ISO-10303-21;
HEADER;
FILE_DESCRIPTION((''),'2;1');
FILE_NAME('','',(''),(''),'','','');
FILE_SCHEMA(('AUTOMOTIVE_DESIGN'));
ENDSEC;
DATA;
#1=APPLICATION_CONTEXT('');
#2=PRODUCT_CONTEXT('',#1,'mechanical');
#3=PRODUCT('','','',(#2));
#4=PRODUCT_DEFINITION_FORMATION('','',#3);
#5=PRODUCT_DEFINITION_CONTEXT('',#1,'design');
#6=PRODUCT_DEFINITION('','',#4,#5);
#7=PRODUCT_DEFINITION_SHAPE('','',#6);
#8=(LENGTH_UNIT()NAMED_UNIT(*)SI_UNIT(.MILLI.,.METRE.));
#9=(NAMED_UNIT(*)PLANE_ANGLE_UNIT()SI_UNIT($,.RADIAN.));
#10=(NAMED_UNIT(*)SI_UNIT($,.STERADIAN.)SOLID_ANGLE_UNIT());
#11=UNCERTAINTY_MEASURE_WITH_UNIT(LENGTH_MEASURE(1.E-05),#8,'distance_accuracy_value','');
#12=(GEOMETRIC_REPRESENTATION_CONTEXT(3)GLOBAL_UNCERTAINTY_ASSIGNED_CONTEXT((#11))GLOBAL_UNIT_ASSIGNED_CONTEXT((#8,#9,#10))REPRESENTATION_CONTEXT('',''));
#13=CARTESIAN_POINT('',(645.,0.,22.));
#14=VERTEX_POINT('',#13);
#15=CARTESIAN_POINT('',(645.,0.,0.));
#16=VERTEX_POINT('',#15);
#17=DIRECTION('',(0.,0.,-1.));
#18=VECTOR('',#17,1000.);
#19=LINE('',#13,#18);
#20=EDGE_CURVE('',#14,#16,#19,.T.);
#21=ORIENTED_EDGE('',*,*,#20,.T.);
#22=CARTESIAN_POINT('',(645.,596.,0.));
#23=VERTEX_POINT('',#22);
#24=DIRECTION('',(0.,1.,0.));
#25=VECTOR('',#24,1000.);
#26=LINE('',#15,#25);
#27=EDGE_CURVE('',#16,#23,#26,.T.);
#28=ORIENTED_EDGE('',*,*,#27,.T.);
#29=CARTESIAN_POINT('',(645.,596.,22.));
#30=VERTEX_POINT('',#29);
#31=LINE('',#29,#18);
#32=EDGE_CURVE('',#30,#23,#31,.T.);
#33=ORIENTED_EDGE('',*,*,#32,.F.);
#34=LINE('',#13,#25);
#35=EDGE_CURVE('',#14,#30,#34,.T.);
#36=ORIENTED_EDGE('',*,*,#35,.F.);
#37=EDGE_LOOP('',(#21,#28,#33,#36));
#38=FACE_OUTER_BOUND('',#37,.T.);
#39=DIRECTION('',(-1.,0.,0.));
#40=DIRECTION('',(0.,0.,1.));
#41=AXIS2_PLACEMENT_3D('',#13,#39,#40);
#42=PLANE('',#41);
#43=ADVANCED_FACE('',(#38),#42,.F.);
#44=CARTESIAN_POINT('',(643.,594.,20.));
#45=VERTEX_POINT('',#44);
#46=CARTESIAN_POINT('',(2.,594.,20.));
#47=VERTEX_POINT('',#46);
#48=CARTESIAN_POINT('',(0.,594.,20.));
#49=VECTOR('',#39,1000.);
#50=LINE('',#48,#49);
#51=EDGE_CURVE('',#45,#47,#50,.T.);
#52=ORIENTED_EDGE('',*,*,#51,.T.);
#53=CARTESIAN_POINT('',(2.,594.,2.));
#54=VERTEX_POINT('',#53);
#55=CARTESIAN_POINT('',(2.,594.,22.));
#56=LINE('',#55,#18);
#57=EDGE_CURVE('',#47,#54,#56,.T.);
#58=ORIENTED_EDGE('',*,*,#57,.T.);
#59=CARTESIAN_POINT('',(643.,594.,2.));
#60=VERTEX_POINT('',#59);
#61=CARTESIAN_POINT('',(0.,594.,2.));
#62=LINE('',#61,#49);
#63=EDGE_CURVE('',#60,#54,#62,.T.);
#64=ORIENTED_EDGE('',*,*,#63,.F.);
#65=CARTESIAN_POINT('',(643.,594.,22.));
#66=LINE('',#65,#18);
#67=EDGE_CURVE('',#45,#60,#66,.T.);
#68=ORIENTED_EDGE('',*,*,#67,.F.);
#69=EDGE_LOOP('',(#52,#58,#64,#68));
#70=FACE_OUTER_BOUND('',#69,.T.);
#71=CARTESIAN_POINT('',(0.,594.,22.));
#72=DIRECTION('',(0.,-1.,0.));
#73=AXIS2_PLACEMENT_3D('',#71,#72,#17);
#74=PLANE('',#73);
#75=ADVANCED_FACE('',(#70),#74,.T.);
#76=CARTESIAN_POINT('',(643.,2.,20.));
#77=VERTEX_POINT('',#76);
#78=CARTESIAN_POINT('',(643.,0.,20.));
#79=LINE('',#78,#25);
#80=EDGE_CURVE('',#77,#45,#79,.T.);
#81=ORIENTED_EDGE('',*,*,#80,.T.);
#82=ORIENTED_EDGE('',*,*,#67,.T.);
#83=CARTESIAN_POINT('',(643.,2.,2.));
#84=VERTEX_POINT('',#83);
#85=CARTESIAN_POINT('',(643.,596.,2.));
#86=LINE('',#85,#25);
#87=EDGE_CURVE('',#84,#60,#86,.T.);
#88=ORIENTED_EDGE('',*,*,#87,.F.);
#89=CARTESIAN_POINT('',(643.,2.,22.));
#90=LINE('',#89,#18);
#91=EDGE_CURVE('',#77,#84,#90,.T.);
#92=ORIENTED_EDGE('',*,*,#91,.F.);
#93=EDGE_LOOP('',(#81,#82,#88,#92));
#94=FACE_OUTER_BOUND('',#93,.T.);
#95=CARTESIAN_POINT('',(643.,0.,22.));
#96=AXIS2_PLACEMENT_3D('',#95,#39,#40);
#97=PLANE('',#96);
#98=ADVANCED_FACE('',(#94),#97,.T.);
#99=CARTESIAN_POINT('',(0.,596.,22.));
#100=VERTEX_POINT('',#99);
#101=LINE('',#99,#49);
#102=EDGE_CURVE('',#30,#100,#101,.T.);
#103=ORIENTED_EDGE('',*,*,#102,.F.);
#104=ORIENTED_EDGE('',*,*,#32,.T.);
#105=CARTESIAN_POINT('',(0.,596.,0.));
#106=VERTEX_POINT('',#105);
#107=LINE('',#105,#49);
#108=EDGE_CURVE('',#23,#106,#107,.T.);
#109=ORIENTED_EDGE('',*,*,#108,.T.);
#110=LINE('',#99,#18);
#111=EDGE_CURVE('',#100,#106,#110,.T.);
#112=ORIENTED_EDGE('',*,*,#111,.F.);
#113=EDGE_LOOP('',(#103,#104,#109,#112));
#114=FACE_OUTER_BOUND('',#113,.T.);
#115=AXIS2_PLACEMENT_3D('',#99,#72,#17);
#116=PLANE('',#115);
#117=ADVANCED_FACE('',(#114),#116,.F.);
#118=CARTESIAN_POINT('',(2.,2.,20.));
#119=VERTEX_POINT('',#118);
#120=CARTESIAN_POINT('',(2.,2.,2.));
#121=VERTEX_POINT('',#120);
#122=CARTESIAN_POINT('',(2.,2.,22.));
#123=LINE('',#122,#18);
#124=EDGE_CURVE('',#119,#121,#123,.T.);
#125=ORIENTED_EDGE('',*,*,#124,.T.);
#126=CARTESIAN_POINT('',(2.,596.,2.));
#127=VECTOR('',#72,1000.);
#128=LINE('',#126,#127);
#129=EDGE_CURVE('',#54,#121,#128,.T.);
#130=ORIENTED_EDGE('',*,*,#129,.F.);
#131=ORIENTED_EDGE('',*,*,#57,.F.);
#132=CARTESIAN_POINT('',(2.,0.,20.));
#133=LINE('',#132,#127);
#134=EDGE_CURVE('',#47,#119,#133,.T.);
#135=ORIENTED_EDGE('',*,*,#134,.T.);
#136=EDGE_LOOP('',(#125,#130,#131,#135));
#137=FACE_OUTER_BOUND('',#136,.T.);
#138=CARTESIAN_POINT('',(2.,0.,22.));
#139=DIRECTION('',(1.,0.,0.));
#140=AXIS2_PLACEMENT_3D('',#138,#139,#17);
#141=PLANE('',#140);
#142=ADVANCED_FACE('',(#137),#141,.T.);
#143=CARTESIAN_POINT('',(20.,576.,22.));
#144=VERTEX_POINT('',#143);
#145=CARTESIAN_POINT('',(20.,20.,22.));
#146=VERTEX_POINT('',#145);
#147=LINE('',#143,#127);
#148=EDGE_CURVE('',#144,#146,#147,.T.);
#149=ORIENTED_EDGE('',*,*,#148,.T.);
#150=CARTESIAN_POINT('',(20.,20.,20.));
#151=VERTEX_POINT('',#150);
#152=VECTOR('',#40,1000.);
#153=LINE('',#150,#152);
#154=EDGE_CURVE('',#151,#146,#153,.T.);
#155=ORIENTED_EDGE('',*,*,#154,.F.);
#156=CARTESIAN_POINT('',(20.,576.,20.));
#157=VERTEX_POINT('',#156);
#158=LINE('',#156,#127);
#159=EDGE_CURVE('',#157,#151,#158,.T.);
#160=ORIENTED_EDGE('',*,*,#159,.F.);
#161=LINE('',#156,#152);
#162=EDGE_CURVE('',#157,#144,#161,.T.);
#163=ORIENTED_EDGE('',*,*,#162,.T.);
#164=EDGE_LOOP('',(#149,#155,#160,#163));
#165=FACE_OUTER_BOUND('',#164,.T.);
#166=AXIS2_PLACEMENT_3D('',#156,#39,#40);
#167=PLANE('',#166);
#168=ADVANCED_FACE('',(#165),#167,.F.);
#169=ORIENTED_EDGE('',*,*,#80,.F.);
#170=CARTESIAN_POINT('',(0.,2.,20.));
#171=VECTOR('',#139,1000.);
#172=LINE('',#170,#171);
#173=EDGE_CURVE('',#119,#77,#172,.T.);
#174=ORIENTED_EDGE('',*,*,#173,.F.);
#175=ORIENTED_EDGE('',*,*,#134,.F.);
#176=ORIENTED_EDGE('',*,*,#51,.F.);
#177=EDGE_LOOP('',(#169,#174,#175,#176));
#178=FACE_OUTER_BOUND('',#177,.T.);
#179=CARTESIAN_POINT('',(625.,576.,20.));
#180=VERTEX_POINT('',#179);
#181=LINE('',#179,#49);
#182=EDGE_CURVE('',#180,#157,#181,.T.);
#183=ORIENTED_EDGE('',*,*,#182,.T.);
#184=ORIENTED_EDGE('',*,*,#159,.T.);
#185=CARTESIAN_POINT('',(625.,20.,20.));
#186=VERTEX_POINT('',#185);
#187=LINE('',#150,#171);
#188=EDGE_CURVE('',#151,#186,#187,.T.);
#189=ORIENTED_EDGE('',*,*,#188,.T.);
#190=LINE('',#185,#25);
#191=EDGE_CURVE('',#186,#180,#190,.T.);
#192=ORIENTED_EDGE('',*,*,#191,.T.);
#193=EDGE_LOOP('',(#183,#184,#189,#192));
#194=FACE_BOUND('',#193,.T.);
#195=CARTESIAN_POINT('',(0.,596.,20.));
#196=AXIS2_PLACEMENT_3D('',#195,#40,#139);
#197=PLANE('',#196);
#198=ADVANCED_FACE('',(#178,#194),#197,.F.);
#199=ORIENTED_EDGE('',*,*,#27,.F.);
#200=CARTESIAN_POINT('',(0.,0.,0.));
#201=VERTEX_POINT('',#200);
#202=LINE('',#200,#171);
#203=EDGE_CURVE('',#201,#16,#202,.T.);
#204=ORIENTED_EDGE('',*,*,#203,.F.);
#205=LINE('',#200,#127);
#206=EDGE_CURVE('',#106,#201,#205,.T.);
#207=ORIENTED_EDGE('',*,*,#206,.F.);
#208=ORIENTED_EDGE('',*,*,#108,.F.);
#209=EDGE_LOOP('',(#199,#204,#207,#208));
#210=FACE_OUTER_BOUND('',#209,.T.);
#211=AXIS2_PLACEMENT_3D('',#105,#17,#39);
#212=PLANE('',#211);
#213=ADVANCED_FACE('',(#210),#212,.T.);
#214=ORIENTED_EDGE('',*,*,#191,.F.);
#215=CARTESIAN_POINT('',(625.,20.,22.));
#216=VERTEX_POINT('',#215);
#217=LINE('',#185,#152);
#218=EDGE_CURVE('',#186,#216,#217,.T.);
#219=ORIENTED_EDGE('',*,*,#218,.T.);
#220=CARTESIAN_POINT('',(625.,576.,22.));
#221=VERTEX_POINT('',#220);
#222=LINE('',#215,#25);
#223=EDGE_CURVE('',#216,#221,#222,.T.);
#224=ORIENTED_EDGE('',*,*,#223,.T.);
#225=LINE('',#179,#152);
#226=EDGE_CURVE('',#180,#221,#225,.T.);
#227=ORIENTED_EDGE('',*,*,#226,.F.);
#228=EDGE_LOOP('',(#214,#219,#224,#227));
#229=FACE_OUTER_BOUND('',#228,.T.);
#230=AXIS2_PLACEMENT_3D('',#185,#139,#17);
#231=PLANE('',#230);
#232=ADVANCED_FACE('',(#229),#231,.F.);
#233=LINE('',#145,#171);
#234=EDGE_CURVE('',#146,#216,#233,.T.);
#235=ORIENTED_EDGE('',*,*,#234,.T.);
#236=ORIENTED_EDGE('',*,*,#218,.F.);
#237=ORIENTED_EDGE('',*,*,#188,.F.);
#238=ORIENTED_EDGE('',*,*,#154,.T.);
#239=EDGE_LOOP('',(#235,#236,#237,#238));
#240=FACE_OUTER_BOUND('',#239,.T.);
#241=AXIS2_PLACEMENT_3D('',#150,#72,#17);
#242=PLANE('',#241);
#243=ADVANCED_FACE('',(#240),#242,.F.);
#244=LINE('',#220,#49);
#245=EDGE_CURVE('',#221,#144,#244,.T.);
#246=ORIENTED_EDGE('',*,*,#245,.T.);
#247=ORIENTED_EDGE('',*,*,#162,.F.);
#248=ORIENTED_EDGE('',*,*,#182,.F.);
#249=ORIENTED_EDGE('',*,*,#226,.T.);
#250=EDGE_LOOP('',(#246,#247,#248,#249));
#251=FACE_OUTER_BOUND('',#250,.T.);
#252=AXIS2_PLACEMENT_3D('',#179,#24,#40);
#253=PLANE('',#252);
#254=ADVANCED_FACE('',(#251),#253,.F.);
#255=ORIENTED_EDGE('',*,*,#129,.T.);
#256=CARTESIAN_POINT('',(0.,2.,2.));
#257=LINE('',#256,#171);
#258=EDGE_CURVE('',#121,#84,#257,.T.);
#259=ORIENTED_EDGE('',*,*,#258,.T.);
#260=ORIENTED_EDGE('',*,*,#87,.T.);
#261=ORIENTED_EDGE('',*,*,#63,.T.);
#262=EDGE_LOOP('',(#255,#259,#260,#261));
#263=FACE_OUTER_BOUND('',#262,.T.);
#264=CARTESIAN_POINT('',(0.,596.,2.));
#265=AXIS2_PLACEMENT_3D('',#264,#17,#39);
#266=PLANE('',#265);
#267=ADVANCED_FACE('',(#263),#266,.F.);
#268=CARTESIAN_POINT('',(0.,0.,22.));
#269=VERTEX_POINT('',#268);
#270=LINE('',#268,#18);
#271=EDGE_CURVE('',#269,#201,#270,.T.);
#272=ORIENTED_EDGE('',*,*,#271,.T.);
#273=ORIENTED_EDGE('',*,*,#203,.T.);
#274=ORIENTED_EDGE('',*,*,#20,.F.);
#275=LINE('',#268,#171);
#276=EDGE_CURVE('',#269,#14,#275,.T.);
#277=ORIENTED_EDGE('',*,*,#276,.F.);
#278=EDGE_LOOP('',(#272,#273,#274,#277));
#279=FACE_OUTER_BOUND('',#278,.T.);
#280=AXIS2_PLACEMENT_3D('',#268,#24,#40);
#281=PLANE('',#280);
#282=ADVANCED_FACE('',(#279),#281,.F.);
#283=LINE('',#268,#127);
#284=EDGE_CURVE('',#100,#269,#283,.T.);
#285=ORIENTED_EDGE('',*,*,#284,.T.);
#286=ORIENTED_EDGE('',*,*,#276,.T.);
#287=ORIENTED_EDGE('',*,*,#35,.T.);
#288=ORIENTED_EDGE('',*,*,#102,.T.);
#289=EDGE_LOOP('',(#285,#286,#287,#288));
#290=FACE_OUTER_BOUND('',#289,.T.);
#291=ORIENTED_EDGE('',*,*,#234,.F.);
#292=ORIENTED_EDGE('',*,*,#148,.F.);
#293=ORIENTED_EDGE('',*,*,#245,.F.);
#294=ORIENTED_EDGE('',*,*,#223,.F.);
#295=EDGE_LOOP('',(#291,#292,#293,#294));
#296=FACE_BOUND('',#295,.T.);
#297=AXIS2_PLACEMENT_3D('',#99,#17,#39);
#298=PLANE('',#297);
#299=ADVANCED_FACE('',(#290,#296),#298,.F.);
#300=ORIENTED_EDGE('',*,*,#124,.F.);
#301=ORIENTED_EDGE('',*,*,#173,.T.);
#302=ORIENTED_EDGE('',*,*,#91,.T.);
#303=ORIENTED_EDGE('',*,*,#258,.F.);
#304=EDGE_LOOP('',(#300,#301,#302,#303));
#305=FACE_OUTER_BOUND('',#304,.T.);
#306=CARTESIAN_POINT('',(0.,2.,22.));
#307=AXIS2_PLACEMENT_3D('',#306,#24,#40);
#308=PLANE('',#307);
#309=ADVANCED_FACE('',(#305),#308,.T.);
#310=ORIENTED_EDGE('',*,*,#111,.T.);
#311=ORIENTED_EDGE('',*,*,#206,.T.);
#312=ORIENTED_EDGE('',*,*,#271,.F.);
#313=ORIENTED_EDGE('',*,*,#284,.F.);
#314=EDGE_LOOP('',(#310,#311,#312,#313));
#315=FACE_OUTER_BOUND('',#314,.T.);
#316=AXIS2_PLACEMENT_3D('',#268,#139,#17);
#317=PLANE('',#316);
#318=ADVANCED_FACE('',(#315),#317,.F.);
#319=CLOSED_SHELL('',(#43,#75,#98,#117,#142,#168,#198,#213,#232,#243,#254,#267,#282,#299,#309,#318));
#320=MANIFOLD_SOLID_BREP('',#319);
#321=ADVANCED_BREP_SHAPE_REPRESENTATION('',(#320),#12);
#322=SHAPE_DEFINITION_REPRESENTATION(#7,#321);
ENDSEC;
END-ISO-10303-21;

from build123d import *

# Parameters (mm, degrees)
SKETCH_1_W      = 645
SKETCH_1_H      = 596
EXTRUDE_1_DEPTH = 22
SHELL_1_T       = -2
SKETCH_2_W      = 645
SKETCH_2_H      = 596
SKETCH_2_W_2    = 605
SKETCH_2_H_2    = 556
EXTRUDE_2_DEPTH = 2


with BuildPart() as part:
    # 草图1 → 凸台-拉伸1 (new body)
    with BuildSketch(Plane.XY):
        with Locations((322.5, 298)):
            Rectangle(SKETCH_1_W, SKETCH_1_H)
    extrude(amount=EXTRUDE_1_DEPTH)

    # 抽壳1
    shell_1_openings = [part.faces().sort_by_distance(p)[0] for p in [
        (322.5, 298, 22),
    ]]
    offset(amount=SHELL_1_T, openings=shell_1_openings, kind=Kind.INTERSECTION)

    # 草图2 → 凸台-拉伸2 (add)
    with BuildSketch(Plane.XY.offset(22)):
        with Locations((322.5, 298)):
            Rectangle(SKETCH_2_W, SKETCH_2_H)
        with Locations((322.5, 298)):
            Rectangle(SKETCH_2_W_2, SKETCH_2_H_2, mode=Mode.SUBTRACT)
    extrude(amount=-EXTRUDE_2_DEPTH)


solid = part.part
